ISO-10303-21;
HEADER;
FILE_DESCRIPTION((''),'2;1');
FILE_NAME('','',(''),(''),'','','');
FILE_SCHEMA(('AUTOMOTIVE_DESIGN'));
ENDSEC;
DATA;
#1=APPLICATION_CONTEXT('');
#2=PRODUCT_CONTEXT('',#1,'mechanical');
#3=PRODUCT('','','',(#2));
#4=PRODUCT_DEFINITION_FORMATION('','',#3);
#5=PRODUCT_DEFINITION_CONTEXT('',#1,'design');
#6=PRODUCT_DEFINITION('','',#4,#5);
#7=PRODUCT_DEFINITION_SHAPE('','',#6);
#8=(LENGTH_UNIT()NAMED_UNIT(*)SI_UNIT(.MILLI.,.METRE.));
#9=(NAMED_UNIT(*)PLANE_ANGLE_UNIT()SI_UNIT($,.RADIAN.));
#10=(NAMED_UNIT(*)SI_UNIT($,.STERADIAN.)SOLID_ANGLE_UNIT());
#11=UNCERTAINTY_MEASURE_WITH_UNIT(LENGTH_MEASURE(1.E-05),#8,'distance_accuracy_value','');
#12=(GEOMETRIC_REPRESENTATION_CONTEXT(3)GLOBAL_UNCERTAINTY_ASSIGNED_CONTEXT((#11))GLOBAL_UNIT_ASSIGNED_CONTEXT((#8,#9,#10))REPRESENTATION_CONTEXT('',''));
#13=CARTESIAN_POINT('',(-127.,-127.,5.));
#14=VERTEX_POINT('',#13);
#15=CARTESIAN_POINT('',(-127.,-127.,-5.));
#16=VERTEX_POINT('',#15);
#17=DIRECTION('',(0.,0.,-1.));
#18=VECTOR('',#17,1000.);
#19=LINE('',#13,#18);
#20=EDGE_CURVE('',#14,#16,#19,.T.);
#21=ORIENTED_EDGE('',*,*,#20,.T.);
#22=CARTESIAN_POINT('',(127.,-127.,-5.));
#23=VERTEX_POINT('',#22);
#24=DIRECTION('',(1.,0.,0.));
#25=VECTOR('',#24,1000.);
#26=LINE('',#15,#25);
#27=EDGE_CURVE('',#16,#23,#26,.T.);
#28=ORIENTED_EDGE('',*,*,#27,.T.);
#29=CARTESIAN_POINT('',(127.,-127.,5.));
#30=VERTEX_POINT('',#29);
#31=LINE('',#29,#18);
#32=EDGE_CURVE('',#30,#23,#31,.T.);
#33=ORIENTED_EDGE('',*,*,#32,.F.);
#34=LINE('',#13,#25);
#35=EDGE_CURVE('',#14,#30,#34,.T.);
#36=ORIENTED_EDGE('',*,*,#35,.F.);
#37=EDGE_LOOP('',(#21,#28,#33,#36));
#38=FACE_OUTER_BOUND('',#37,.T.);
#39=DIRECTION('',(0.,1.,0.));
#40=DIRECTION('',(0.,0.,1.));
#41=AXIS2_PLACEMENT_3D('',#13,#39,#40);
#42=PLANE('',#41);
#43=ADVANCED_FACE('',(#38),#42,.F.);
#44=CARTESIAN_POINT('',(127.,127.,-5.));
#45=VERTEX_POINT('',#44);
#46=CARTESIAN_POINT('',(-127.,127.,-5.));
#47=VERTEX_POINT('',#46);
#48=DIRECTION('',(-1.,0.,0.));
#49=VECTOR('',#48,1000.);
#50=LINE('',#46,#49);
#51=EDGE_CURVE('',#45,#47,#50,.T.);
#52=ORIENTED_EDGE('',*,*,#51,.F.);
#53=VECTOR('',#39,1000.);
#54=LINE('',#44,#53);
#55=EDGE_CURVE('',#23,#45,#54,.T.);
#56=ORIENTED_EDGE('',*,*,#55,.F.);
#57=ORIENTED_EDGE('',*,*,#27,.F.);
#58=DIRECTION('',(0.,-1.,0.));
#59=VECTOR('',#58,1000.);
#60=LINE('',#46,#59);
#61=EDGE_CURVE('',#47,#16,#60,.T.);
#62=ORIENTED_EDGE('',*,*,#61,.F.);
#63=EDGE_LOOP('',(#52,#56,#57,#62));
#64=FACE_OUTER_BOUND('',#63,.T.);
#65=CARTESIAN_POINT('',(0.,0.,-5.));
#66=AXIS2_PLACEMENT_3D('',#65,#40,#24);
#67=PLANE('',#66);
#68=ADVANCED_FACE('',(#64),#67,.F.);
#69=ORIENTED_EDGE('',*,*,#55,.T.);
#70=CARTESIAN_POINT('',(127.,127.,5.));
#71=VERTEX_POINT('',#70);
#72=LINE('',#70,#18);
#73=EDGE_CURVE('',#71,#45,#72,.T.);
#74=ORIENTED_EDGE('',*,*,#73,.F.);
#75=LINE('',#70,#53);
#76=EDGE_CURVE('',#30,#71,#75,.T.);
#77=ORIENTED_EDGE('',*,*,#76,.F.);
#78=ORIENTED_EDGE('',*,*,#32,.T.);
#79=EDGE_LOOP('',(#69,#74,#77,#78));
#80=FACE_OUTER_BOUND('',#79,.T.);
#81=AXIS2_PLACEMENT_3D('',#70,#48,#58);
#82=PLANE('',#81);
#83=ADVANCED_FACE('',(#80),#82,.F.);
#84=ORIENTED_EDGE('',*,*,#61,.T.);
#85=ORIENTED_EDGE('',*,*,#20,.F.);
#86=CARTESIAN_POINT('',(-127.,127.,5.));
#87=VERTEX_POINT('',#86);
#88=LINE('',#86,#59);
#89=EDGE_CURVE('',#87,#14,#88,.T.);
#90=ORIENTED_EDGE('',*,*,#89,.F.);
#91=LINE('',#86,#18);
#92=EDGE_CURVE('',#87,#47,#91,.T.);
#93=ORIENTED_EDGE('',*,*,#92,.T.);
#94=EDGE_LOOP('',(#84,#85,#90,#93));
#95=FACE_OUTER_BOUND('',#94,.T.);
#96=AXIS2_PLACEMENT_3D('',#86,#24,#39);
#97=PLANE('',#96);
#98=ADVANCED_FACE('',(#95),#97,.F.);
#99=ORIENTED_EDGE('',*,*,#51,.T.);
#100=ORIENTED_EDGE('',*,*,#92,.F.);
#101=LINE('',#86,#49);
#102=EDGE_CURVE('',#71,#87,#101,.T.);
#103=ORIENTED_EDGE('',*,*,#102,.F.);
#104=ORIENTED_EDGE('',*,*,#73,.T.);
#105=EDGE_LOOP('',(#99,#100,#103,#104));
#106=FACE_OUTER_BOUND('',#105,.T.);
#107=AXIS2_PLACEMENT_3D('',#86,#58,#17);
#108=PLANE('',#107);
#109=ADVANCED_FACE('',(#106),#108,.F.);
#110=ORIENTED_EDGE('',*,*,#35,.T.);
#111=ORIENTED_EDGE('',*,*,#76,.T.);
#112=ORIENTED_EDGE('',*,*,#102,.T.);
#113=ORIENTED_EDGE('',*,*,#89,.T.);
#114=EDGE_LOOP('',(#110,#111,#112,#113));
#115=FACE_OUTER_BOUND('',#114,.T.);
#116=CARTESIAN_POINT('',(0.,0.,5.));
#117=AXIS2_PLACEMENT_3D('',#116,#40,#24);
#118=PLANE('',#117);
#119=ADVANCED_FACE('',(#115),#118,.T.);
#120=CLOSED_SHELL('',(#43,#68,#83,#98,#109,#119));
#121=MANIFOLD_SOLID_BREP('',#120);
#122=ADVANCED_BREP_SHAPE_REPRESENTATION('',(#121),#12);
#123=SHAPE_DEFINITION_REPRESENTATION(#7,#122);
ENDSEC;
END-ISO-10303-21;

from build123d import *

# Parameters (mm, degrees)
SKETCH1_W           = 254
SKETCH1_H           = 254
BOSS_EXTRUDE1_DEPTH = 5


with BuildPart() as part:
    # Sketch1 → Boss-Extrude1 (new, symmetric)
    with BuildSketch(Plane.XY):
        Rectangle(SKETCH1_W, SKETCH1_H)
    extrude(amount=BOSS_EXTRUDE1_DEPTH, both=True)


solid = part.part
